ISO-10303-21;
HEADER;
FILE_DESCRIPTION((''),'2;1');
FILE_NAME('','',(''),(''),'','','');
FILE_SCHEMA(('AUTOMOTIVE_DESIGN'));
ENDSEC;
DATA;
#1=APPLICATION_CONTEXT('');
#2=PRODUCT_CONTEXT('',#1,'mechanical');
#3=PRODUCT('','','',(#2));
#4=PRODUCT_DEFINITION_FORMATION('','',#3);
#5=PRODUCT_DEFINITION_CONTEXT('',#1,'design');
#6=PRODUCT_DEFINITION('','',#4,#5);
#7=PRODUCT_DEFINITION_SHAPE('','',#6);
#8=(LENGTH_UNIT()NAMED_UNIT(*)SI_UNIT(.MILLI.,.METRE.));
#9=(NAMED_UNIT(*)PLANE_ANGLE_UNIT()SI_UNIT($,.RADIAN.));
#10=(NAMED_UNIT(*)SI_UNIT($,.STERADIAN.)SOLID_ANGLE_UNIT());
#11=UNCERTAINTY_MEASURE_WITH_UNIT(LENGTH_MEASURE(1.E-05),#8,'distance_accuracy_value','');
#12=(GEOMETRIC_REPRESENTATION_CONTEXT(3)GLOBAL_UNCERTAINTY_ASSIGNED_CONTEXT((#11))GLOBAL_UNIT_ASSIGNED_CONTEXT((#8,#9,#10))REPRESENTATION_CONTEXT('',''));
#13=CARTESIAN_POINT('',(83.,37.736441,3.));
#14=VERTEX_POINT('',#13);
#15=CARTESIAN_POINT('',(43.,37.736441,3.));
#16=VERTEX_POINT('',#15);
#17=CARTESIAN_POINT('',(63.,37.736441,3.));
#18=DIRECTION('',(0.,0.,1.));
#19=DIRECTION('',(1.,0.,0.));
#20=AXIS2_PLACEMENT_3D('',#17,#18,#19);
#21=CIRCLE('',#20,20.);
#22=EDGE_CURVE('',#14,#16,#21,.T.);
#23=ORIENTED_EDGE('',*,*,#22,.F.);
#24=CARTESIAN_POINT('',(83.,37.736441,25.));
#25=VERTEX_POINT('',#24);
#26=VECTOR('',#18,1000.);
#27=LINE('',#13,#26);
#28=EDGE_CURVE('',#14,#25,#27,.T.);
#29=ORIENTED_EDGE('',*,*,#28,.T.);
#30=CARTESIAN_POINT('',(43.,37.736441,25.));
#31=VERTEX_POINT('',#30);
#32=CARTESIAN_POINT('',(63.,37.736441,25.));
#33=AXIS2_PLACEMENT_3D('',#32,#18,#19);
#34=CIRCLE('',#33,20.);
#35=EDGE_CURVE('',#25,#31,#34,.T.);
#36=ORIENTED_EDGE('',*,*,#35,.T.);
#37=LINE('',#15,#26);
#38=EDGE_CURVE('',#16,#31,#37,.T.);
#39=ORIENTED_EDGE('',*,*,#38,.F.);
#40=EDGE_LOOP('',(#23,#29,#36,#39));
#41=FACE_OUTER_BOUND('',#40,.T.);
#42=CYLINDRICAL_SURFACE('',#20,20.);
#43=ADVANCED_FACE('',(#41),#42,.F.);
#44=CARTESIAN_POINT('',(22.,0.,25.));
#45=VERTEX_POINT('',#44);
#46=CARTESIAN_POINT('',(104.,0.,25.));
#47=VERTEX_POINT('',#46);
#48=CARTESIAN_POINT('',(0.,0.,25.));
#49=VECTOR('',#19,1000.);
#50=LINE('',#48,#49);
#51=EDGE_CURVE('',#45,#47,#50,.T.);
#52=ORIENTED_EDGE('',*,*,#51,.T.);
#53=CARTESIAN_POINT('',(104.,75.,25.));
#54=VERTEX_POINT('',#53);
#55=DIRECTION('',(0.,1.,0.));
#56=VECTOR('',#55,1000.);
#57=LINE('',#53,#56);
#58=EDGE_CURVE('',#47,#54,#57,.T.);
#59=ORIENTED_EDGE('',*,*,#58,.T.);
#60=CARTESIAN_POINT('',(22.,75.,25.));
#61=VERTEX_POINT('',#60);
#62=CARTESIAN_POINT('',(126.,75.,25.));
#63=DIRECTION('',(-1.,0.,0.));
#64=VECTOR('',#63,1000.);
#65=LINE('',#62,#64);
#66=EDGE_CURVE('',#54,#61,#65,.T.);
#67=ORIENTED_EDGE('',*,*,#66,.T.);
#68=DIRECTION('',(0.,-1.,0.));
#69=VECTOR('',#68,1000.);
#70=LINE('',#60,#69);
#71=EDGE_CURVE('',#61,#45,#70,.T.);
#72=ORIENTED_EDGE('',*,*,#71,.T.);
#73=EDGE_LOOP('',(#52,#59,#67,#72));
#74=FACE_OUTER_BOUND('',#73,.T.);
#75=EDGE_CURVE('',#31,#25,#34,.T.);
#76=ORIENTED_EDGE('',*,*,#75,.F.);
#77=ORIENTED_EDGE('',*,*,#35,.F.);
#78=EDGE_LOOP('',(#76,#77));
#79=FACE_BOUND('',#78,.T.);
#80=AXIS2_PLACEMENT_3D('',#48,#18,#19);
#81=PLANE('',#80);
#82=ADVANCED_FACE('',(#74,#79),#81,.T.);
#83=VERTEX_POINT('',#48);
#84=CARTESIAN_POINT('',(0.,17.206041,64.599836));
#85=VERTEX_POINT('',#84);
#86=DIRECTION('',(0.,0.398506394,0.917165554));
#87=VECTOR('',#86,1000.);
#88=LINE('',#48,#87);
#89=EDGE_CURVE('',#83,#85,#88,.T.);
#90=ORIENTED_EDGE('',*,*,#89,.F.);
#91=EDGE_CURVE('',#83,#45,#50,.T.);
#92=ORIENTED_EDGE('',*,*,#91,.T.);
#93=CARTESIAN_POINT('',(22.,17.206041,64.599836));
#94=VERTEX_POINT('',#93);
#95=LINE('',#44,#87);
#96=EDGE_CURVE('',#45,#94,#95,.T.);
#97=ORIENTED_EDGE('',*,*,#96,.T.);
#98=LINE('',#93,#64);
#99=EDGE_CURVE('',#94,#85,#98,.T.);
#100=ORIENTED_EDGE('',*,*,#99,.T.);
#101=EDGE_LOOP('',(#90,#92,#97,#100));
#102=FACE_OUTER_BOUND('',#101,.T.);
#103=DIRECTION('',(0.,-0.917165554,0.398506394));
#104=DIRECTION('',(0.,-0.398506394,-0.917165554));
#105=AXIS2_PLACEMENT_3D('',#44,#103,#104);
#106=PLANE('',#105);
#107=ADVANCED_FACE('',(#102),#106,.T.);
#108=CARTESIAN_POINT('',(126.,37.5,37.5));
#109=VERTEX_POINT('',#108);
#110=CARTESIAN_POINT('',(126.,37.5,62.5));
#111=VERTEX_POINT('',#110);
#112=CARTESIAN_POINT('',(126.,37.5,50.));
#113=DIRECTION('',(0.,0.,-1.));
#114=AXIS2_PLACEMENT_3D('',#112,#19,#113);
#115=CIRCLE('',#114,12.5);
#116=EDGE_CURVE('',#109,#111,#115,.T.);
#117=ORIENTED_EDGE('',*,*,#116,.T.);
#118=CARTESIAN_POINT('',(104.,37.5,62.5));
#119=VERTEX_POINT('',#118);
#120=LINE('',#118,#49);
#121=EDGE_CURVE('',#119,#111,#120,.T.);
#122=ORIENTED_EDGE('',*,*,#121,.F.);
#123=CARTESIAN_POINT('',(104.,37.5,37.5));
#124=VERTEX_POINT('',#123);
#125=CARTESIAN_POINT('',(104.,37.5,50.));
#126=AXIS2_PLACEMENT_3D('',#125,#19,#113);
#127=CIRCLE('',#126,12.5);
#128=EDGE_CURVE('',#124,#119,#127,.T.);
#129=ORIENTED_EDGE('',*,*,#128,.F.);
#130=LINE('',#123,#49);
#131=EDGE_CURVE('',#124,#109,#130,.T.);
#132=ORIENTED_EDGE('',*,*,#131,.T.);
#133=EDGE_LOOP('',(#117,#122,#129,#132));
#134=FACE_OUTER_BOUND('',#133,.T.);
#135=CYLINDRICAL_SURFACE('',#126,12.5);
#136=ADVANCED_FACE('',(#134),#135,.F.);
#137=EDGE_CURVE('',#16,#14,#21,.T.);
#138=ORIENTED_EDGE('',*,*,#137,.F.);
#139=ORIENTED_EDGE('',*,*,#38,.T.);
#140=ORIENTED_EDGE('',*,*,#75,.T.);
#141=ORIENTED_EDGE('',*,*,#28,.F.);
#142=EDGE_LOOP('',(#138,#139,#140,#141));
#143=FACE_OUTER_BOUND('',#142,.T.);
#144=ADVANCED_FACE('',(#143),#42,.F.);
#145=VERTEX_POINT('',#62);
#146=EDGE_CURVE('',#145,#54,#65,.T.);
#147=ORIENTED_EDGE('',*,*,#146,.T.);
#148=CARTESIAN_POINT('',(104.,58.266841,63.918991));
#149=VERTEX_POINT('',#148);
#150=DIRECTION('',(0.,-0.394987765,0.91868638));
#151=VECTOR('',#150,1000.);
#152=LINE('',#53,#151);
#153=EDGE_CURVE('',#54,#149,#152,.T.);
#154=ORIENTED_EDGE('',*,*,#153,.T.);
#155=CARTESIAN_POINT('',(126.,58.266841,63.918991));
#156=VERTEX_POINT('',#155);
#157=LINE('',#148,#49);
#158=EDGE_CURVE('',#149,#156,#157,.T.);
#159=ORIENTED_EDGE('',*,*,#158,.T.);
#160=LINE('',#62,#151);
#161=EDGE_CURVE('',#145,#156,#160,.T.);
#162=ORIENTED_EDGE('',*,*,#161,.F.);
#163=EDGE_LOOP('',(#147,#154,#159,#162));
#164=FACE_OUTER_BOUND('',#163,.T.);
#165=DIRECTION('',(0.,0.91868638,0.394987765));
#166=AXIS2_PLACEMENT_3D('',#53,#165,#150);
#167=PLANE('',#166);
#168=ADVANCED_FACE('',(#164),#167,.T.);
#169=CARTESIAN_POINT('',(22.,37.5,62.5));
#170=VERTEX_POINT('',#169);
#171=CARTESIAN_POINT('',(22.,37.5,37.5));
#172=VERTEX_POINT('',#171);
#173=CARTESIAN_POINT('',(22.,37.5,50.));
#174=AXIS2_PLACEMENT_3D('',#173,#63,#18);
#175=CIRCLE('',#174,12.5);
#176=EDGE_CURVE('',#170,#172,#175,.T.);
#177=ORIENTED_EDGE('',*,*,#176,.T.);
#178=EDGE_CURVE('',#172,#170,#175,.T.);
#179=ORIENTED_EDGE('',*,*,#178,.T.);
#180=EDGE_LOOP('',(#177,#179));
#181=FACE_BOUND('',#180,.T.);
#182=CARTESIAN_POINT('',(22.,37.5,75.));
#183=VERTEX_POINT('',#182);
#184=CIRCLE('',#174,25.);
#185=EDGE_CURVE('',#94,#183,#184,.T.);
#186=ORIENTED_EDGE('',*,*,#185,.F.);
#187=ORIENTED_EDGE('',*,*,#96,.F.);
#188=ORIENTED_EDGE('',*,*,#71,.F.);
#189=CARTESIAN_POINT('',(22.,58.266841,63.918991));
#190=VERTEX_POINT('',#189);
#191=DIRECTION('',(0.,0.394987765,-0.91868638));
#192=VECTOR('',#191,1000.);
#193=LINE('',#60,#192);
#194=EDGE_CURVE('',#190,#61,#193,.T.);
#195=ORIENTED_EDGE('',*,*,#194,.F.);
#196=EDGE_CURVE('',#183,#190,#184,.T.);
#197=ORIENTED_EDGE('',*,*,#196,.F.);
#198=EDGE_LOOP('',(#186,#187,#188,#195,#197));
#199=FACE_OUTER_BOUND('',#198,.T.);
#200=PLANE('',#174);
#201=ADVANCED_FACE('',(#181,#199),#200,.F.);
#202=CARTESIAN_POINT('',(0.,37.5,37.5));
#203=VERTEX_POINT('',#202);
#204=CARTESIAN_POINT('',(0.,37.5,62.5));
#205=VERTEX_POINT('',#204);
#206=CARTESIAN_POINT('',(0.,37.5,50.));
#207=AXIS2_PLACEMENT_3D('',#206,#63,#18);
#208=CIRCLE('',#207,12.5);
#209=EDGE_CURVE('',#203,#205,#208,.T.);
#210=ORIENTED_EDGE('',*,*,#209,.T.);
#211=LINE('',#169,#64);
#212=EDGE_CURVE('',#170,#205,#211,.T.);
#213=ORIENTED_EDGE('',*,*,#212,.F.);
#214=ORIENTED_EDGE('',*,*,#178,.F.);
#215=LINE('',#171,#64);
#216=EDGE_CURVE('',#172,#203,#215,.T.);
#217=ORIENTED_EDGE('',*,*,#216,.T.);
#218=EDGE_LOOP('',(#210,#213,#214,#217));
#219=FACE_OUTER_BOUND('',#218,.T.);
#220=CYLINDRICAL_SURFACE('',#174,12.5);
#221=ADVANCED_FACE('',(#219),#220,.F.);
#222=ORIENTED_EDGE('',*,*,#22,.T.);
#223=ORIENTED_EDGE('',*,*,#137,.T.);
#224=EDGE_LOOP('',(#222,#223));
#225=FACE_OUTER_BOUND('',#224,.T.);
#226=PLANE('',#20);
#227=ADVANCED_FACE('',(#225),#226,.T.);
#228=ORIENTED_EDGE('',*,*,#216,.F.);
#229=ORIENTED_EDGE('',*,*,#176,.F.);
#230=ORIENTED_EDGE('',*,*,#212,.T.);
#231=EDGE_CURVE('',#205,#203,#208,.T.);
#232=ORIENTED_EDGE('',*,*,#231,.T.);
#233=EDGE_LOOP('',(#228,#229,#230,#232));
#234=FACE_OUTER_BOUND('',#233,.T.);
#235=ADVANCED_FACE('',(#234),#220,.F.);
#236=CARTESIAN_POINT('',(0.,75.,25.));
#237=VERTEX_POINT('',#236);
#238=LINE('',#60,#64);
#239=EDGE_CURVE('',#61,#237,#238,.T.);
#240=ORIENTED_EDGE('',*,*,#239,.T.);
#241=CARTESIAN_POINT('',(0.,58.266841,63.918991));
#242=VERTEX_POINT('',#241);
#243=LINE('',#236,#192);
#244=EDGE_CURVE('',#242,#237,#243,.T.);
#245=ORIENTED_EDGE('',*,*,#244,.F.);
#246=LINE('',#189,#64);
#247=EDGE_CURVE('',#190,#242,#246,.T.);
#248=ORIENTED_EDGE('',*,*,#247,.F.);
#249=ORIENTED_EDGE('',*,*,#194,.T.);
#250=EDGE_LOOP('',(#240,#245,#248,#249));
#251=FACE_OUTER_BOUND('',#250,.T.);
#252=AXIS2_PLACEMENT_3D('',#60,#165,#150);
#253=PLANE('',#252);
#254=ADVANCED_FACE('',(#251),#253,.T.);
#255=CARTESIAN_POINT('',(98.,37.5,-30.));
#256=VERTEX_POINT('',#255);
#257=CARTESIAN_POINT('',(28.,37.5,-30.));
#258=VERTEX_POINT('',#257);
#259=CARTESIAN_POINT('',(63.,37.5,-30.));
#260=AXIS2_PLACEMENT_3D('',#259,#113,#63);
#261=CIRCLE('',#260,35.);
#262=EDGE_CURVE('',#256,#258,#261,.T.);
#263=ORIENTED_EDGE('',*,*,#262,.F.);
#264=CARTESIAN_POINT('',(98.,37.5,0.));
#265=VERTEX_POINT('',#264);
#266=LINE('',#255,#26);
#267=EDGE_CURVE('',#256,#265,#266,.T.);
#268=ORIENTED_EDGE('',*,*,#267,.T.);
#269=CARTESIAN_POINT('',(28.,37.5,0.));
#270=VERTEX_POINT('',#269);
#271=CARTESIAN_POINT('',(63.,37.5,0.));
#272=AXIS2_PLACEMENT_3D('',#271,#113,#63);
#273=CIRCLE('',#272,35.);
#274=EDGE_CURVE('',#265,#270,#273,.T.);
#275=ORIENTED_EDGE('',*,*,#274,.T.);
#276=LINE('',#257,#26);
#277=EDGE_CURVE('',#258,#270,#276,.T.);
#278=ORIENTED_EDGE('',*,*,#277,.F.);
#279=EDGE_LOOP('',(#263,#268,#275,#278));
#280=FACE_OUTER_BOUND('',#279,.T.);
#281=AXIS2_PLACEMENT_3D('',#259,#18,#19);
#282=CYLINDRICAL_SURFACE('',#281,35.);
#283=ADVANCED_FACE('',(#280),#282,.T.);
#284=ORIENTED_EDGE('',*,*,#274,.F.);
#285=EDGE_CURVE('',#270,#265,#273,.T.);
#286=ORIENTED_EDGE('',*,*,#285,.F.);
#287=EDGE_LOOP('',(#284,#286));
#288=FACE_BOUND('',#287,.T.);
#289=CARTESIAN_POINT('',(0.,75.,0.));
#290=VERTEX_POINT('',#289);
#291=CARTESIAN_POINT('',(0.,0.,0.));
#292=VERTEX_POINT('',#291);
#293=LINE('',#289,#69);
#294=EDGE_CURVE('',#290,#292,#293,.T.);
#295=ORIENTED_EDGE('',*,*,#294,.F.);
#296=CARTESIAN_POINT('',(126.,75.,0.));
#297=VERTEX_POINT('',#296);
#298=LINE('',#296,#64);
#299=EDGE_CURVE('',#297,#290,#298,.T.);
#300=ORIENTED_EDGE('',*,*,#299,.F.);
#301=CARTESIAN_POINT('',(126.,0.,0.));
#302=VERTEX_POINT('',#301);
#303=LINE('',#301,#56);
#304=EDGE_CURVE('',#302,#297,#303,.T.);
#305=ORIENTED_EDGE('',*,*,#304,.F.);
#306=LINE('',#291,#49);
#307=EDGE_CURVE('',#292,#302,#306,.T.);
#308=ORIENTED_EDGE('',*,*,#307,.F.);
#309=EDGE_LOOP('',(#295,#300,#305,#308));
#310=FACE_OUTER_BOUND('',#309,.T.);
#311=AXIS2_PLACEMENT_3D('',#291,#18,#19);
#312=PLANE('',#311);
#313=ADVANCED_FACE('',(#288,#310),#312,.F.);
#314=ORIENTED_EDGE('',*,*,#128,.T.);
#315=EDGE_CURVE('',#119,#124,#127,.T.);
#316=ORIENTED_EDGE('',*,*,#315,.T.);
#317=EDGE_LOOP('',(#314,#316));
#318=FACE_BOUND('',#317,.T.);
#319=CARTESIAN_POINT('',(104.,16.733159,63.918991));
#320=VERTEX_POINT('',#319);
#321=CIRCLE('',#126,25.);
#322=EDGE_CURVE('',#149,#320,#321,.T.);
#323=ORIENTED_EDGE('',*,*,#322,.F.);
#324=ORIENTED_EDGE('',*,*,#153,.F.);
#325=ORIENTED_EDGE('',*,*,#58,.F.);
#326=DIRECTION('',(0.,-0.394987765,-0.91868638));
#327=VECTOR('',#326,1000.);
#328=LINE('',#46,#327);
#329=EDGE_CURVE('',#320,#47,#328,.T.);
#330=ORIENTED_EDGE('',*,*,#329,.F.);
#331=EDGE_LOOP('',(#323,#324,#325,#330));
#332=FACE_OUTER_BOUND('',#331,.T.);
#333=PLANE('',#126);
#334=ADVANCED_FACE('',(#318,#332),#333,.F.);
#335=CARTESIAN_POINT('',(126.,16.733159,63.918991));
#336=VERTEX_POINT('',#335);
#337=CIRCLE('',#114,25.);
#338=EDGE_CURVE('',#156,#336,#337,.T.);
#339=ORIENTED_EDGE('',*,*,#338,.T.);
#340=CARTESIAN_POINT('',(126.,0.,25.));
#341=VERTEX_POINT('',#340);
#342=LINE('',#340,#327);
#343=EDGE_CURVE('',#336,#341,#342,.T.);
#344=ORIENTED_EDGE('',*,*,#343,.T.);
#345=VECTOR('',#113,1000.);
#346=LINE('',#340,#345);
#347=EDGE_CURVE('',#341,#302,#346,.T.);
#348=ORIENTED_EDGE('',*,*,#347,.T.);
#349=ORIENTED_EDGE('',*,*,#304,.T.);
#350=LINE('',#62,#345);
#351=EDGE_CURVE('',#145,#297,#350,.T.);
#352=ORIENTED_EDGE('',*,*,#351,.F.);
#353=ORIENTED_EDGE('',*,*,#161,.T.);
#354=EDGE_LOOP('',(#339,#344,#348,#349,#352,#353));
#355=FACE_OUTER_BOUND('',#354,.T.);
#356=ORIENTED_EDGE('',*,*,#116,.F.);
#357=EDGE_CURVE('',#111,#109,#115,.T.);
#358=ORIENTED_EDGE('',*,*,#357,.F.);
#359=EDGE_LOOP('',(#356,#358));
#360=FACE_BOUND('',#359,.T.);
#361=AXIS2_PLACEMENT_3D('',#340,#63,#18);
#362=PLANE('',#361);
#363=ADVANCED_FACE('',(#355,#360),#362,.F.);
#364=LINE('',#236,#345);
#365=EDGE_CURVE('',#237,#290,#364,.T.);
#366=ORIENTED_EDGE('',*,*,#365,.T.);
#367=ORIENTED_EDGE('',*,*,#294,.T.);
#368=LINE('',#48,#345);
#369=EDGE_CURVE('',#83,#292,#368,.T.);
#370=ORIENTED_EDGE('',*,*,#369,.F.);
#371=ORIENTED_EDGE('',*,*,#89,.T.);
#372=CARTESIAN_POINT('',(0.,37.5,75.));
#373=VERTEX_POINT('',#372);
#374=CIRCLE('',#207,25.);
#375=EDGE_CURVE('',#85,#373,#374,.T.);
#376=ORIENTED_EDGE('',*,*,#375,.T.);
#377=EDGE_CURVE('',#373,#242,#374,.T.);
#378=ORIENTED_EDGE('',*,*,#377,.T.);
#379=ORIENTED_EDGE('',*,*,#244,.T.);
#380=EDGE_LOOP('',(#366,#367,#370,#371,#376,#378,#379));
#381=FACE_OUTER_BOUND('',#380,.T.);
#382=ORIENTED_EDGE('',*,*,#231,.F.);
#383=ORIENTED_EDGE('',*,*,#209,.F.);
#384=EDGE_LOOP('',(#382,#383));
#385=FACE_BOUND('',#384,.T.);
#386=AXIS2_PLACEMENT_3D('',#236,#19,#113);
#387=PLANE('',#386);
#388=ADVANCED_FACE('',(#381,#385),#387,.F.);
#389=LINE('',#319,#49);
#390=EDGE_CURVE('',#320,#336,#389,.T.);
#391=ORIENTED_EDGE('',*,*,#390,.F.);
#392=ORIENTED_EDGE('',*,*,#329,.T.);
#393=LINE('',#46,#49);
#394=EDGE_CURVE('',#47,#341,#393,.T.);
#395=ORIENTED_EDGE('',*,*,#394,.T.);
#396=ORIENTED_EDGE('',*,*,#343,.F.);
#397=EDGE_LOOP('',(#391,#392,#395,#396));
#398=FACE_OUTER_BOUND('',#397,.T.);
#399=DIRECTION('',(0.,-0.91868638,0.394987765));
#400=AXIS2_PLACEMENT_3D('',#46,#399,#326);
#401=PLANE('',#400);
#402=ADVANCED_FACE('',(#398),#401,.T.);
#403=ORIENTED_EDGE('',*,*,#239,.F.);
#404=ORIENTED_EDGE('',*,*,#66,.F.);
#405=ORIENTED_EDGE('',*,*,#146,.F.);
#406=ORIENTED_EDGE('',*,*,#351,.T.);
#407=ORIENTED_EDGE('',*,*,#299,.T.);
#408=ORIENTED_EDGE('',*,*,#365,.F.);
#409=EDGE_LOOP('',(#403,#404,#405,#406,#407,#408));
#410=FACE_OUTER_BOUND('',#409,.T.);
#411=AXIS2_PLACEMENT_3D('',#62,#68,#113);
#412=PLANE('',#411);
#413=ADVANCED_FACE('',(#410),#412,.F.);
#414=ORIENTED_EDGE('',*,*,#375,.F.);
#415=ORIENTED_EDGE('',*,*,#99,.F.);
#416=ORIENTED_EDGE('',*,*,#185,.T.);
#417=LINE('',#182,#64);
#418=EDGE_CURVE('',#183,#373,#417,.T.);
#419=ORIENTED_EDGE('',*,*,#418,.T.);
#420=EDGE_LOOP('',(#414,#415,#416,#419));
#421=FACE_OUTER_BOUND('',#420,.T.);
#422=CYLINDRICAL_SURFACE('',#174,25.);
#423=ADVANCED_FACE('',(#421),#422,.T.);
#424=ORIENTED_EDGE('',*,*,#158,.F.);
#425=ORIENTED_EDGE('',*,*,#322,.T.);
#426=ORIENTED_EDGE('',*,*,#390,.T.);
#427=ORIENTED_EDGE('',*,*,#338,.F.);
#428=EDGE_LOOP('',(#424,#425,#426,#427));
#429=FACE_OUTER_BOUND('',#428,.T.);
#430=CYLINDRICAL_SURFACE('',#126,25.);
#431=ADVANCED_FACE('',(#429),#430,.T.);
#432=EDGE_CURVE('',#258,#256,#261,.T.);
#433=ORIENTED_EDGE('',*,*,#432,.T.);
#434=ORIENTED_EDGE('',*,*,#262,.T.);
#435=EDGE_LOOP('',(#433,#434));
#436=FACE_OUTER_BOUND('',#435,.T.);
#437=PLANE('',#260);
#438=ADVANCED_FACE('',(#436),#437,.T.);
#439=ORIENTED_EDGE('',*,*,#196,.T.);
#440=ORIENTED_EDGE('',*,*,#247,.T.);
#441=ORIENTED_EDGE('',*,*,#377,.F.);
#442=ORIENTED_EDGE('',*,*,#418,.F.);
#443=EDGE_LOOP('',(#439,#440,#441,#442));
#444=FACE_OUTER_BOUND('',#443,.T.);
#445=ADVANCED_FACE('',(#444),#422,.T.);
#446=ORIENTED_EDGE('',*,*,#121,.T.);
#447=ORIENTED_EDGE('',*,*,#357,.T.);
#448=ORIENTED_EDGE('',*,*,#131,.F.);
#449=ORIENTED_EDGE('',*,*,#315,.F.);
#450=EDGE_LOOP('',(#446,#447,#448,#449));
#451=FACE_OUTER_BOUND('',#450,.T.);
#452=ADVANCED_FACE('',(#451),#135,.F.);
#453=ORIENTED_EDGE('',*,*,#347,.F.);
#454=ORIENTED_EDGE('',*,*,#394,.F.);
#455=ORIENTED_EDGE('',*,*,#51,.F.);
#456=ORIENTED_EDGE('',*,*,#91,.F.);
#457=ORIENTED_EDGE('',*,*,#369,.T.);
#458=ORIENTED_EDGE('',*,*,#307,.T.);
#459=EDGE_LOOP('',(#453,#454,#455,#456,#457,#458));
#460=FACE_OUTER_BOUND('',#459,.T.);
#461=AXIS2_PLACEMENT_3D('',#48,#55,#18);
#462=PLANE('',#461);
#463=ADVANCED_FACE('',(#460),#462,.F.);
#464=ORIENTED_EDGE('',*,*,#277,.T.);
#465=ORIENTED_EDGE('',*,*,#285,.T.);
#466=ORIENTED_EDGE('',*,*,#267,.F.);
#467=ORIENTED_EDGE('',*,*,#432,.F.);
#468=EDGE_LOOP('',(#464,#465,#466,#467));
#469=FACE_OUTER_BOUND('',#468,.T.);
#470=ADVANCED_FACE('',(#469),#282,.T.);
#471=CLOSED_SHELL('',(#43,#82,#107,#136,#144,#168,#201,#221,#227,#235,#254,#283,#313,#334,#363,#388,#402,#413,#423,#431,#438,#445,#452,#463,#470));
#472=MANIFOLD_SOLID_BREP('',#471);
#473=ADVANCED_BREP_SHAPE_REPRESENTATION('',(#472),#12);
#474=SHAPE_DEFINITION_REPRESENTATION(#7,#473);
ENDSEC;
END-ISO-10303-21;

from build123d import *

# Parameters (mm, degrees)
BASE_PLATE_SKETCH_W  = 126
BASE_PLATE_SKETCH_H  = 75
BASE_PLATE_DEPTH     = 25
LUG_1_DEPTH          = 22
LUG_START            = -22
LUG_2_DEPTH          = 22
CENTRE_BORE_SKETCH_R = 20
CENTRE_BORE_40_DEPTH = 22
REAR_BOSS_SKETCH_R   = 35
REAR_BOSS_70_DEPTH   = 30
LUG_HOLE_1_SKETCH_R  = 12.5
LUG_HOLE_1_25_DEPTH  = 22
LUG_HOLE_2_SKETCH_R  = 12.5
LUG_HOLE_2_25_DEPTH  = 22


with BuildPart() as part:
    # Base Plate Sketch → Base Plate (new body)
    with BuildSketch(Plane.XY):
        with Locations((63, 37.5)):
            Rectangle(BASE_PLATE_SKETCH_W, BASE_PLATE_SKETCH_H)
    extrude(amount=BASE_PLATE_DEPTH)

    # Lug 1 Sketch → Lug 1 (add)
    with BuildSketch(Plane(origin=(126, 0, 0), x_dir=(0, 0, -1), z_dir=(1, 0, 0))):
        with BuildLine():
            Line((-25, 75), (-25, 0))
            Line((-25, 0), (-63.918991375, 16.733159145))
            ThreePointArc((-63.918991375, 16.733159145), (-75, 37.5), (-63.918991375, 58.266840855))
            Line((-63.918991375, 58.266840855), (-25, 75))
        make_face()
    extrude(amount=-LUG_1_DEPTH)

    # Lug 2 Sketch → Lug 2 (add)
    with BuildSketch(Plane.ZY.offset(LUG_START)):
        with BuildLine():
            Line((25, 75), (25, 0))
            Line((25, 0), (64.599836332, 17.206040823))
            ThreePointArc((64.599836332, 17.206040823), (74.996563929, 37.914477664), (63.918991375, 58.266840855))
            Line((63.918991375, 58.266840855), (25, 75))
        make_face()
    extrude(amount=LUG_2_DEPTH)

    # Centre Bore Sketch → Centre Bore Ø40 (cut)
    with BuildSketch(Plane.XY.offset(25)):
        with Locations((63, 37.736440839)):
            Circle(CENTRE_BORE_SKETCH_R)
    extrude(amount=-CENTRE_BORE_40_DEPTH, mode=Mode.SUBTRACT)

    # Rear Boss Sketch → Rear Boss Ø70 (add)
    with BuildSketch(Plane(origin=(0, 0, 0), x_dir=(-1, 0, 0), z_dir=(0, 0, -1))):
        with Locations((-63, 37.5)):
            Circle(REAR_BOSS_SKETCH_R)
    extrude(amount=REAR_BOSS_70_DEPTH)

    # Lug Hole 1 Sketch → Lug Hole 1 Ø25 (cut)
    with BuildSketch(Plane.ZY):
        with Locations((50, 37.5)):
            Circle(LUG_HOLE_1_SKETCH_R)
    extrude(amount=-LUG_HOLE_1_25_DEPTH, mode=Mode.SUBTRACT)

    # Lug Hole 2 Sketch → Lug Hole 2 Ø25 (cut)
    with BuildSketch(Plane(origin=(126, 0, 0), x_dir=(0, 0, -1), z_dir=(1, 0, 0)).offset(LUG_START)):
        with Locations(Location((-50, 37.5, 0), (0, 0, 180))):
            Circle(LUG_HOLE_2_SKETCH_R)
    extrude(amount=LUG_HOLE_2_25_DEPTH, mode=Mode.SUBTRACT)


solid = part.part
